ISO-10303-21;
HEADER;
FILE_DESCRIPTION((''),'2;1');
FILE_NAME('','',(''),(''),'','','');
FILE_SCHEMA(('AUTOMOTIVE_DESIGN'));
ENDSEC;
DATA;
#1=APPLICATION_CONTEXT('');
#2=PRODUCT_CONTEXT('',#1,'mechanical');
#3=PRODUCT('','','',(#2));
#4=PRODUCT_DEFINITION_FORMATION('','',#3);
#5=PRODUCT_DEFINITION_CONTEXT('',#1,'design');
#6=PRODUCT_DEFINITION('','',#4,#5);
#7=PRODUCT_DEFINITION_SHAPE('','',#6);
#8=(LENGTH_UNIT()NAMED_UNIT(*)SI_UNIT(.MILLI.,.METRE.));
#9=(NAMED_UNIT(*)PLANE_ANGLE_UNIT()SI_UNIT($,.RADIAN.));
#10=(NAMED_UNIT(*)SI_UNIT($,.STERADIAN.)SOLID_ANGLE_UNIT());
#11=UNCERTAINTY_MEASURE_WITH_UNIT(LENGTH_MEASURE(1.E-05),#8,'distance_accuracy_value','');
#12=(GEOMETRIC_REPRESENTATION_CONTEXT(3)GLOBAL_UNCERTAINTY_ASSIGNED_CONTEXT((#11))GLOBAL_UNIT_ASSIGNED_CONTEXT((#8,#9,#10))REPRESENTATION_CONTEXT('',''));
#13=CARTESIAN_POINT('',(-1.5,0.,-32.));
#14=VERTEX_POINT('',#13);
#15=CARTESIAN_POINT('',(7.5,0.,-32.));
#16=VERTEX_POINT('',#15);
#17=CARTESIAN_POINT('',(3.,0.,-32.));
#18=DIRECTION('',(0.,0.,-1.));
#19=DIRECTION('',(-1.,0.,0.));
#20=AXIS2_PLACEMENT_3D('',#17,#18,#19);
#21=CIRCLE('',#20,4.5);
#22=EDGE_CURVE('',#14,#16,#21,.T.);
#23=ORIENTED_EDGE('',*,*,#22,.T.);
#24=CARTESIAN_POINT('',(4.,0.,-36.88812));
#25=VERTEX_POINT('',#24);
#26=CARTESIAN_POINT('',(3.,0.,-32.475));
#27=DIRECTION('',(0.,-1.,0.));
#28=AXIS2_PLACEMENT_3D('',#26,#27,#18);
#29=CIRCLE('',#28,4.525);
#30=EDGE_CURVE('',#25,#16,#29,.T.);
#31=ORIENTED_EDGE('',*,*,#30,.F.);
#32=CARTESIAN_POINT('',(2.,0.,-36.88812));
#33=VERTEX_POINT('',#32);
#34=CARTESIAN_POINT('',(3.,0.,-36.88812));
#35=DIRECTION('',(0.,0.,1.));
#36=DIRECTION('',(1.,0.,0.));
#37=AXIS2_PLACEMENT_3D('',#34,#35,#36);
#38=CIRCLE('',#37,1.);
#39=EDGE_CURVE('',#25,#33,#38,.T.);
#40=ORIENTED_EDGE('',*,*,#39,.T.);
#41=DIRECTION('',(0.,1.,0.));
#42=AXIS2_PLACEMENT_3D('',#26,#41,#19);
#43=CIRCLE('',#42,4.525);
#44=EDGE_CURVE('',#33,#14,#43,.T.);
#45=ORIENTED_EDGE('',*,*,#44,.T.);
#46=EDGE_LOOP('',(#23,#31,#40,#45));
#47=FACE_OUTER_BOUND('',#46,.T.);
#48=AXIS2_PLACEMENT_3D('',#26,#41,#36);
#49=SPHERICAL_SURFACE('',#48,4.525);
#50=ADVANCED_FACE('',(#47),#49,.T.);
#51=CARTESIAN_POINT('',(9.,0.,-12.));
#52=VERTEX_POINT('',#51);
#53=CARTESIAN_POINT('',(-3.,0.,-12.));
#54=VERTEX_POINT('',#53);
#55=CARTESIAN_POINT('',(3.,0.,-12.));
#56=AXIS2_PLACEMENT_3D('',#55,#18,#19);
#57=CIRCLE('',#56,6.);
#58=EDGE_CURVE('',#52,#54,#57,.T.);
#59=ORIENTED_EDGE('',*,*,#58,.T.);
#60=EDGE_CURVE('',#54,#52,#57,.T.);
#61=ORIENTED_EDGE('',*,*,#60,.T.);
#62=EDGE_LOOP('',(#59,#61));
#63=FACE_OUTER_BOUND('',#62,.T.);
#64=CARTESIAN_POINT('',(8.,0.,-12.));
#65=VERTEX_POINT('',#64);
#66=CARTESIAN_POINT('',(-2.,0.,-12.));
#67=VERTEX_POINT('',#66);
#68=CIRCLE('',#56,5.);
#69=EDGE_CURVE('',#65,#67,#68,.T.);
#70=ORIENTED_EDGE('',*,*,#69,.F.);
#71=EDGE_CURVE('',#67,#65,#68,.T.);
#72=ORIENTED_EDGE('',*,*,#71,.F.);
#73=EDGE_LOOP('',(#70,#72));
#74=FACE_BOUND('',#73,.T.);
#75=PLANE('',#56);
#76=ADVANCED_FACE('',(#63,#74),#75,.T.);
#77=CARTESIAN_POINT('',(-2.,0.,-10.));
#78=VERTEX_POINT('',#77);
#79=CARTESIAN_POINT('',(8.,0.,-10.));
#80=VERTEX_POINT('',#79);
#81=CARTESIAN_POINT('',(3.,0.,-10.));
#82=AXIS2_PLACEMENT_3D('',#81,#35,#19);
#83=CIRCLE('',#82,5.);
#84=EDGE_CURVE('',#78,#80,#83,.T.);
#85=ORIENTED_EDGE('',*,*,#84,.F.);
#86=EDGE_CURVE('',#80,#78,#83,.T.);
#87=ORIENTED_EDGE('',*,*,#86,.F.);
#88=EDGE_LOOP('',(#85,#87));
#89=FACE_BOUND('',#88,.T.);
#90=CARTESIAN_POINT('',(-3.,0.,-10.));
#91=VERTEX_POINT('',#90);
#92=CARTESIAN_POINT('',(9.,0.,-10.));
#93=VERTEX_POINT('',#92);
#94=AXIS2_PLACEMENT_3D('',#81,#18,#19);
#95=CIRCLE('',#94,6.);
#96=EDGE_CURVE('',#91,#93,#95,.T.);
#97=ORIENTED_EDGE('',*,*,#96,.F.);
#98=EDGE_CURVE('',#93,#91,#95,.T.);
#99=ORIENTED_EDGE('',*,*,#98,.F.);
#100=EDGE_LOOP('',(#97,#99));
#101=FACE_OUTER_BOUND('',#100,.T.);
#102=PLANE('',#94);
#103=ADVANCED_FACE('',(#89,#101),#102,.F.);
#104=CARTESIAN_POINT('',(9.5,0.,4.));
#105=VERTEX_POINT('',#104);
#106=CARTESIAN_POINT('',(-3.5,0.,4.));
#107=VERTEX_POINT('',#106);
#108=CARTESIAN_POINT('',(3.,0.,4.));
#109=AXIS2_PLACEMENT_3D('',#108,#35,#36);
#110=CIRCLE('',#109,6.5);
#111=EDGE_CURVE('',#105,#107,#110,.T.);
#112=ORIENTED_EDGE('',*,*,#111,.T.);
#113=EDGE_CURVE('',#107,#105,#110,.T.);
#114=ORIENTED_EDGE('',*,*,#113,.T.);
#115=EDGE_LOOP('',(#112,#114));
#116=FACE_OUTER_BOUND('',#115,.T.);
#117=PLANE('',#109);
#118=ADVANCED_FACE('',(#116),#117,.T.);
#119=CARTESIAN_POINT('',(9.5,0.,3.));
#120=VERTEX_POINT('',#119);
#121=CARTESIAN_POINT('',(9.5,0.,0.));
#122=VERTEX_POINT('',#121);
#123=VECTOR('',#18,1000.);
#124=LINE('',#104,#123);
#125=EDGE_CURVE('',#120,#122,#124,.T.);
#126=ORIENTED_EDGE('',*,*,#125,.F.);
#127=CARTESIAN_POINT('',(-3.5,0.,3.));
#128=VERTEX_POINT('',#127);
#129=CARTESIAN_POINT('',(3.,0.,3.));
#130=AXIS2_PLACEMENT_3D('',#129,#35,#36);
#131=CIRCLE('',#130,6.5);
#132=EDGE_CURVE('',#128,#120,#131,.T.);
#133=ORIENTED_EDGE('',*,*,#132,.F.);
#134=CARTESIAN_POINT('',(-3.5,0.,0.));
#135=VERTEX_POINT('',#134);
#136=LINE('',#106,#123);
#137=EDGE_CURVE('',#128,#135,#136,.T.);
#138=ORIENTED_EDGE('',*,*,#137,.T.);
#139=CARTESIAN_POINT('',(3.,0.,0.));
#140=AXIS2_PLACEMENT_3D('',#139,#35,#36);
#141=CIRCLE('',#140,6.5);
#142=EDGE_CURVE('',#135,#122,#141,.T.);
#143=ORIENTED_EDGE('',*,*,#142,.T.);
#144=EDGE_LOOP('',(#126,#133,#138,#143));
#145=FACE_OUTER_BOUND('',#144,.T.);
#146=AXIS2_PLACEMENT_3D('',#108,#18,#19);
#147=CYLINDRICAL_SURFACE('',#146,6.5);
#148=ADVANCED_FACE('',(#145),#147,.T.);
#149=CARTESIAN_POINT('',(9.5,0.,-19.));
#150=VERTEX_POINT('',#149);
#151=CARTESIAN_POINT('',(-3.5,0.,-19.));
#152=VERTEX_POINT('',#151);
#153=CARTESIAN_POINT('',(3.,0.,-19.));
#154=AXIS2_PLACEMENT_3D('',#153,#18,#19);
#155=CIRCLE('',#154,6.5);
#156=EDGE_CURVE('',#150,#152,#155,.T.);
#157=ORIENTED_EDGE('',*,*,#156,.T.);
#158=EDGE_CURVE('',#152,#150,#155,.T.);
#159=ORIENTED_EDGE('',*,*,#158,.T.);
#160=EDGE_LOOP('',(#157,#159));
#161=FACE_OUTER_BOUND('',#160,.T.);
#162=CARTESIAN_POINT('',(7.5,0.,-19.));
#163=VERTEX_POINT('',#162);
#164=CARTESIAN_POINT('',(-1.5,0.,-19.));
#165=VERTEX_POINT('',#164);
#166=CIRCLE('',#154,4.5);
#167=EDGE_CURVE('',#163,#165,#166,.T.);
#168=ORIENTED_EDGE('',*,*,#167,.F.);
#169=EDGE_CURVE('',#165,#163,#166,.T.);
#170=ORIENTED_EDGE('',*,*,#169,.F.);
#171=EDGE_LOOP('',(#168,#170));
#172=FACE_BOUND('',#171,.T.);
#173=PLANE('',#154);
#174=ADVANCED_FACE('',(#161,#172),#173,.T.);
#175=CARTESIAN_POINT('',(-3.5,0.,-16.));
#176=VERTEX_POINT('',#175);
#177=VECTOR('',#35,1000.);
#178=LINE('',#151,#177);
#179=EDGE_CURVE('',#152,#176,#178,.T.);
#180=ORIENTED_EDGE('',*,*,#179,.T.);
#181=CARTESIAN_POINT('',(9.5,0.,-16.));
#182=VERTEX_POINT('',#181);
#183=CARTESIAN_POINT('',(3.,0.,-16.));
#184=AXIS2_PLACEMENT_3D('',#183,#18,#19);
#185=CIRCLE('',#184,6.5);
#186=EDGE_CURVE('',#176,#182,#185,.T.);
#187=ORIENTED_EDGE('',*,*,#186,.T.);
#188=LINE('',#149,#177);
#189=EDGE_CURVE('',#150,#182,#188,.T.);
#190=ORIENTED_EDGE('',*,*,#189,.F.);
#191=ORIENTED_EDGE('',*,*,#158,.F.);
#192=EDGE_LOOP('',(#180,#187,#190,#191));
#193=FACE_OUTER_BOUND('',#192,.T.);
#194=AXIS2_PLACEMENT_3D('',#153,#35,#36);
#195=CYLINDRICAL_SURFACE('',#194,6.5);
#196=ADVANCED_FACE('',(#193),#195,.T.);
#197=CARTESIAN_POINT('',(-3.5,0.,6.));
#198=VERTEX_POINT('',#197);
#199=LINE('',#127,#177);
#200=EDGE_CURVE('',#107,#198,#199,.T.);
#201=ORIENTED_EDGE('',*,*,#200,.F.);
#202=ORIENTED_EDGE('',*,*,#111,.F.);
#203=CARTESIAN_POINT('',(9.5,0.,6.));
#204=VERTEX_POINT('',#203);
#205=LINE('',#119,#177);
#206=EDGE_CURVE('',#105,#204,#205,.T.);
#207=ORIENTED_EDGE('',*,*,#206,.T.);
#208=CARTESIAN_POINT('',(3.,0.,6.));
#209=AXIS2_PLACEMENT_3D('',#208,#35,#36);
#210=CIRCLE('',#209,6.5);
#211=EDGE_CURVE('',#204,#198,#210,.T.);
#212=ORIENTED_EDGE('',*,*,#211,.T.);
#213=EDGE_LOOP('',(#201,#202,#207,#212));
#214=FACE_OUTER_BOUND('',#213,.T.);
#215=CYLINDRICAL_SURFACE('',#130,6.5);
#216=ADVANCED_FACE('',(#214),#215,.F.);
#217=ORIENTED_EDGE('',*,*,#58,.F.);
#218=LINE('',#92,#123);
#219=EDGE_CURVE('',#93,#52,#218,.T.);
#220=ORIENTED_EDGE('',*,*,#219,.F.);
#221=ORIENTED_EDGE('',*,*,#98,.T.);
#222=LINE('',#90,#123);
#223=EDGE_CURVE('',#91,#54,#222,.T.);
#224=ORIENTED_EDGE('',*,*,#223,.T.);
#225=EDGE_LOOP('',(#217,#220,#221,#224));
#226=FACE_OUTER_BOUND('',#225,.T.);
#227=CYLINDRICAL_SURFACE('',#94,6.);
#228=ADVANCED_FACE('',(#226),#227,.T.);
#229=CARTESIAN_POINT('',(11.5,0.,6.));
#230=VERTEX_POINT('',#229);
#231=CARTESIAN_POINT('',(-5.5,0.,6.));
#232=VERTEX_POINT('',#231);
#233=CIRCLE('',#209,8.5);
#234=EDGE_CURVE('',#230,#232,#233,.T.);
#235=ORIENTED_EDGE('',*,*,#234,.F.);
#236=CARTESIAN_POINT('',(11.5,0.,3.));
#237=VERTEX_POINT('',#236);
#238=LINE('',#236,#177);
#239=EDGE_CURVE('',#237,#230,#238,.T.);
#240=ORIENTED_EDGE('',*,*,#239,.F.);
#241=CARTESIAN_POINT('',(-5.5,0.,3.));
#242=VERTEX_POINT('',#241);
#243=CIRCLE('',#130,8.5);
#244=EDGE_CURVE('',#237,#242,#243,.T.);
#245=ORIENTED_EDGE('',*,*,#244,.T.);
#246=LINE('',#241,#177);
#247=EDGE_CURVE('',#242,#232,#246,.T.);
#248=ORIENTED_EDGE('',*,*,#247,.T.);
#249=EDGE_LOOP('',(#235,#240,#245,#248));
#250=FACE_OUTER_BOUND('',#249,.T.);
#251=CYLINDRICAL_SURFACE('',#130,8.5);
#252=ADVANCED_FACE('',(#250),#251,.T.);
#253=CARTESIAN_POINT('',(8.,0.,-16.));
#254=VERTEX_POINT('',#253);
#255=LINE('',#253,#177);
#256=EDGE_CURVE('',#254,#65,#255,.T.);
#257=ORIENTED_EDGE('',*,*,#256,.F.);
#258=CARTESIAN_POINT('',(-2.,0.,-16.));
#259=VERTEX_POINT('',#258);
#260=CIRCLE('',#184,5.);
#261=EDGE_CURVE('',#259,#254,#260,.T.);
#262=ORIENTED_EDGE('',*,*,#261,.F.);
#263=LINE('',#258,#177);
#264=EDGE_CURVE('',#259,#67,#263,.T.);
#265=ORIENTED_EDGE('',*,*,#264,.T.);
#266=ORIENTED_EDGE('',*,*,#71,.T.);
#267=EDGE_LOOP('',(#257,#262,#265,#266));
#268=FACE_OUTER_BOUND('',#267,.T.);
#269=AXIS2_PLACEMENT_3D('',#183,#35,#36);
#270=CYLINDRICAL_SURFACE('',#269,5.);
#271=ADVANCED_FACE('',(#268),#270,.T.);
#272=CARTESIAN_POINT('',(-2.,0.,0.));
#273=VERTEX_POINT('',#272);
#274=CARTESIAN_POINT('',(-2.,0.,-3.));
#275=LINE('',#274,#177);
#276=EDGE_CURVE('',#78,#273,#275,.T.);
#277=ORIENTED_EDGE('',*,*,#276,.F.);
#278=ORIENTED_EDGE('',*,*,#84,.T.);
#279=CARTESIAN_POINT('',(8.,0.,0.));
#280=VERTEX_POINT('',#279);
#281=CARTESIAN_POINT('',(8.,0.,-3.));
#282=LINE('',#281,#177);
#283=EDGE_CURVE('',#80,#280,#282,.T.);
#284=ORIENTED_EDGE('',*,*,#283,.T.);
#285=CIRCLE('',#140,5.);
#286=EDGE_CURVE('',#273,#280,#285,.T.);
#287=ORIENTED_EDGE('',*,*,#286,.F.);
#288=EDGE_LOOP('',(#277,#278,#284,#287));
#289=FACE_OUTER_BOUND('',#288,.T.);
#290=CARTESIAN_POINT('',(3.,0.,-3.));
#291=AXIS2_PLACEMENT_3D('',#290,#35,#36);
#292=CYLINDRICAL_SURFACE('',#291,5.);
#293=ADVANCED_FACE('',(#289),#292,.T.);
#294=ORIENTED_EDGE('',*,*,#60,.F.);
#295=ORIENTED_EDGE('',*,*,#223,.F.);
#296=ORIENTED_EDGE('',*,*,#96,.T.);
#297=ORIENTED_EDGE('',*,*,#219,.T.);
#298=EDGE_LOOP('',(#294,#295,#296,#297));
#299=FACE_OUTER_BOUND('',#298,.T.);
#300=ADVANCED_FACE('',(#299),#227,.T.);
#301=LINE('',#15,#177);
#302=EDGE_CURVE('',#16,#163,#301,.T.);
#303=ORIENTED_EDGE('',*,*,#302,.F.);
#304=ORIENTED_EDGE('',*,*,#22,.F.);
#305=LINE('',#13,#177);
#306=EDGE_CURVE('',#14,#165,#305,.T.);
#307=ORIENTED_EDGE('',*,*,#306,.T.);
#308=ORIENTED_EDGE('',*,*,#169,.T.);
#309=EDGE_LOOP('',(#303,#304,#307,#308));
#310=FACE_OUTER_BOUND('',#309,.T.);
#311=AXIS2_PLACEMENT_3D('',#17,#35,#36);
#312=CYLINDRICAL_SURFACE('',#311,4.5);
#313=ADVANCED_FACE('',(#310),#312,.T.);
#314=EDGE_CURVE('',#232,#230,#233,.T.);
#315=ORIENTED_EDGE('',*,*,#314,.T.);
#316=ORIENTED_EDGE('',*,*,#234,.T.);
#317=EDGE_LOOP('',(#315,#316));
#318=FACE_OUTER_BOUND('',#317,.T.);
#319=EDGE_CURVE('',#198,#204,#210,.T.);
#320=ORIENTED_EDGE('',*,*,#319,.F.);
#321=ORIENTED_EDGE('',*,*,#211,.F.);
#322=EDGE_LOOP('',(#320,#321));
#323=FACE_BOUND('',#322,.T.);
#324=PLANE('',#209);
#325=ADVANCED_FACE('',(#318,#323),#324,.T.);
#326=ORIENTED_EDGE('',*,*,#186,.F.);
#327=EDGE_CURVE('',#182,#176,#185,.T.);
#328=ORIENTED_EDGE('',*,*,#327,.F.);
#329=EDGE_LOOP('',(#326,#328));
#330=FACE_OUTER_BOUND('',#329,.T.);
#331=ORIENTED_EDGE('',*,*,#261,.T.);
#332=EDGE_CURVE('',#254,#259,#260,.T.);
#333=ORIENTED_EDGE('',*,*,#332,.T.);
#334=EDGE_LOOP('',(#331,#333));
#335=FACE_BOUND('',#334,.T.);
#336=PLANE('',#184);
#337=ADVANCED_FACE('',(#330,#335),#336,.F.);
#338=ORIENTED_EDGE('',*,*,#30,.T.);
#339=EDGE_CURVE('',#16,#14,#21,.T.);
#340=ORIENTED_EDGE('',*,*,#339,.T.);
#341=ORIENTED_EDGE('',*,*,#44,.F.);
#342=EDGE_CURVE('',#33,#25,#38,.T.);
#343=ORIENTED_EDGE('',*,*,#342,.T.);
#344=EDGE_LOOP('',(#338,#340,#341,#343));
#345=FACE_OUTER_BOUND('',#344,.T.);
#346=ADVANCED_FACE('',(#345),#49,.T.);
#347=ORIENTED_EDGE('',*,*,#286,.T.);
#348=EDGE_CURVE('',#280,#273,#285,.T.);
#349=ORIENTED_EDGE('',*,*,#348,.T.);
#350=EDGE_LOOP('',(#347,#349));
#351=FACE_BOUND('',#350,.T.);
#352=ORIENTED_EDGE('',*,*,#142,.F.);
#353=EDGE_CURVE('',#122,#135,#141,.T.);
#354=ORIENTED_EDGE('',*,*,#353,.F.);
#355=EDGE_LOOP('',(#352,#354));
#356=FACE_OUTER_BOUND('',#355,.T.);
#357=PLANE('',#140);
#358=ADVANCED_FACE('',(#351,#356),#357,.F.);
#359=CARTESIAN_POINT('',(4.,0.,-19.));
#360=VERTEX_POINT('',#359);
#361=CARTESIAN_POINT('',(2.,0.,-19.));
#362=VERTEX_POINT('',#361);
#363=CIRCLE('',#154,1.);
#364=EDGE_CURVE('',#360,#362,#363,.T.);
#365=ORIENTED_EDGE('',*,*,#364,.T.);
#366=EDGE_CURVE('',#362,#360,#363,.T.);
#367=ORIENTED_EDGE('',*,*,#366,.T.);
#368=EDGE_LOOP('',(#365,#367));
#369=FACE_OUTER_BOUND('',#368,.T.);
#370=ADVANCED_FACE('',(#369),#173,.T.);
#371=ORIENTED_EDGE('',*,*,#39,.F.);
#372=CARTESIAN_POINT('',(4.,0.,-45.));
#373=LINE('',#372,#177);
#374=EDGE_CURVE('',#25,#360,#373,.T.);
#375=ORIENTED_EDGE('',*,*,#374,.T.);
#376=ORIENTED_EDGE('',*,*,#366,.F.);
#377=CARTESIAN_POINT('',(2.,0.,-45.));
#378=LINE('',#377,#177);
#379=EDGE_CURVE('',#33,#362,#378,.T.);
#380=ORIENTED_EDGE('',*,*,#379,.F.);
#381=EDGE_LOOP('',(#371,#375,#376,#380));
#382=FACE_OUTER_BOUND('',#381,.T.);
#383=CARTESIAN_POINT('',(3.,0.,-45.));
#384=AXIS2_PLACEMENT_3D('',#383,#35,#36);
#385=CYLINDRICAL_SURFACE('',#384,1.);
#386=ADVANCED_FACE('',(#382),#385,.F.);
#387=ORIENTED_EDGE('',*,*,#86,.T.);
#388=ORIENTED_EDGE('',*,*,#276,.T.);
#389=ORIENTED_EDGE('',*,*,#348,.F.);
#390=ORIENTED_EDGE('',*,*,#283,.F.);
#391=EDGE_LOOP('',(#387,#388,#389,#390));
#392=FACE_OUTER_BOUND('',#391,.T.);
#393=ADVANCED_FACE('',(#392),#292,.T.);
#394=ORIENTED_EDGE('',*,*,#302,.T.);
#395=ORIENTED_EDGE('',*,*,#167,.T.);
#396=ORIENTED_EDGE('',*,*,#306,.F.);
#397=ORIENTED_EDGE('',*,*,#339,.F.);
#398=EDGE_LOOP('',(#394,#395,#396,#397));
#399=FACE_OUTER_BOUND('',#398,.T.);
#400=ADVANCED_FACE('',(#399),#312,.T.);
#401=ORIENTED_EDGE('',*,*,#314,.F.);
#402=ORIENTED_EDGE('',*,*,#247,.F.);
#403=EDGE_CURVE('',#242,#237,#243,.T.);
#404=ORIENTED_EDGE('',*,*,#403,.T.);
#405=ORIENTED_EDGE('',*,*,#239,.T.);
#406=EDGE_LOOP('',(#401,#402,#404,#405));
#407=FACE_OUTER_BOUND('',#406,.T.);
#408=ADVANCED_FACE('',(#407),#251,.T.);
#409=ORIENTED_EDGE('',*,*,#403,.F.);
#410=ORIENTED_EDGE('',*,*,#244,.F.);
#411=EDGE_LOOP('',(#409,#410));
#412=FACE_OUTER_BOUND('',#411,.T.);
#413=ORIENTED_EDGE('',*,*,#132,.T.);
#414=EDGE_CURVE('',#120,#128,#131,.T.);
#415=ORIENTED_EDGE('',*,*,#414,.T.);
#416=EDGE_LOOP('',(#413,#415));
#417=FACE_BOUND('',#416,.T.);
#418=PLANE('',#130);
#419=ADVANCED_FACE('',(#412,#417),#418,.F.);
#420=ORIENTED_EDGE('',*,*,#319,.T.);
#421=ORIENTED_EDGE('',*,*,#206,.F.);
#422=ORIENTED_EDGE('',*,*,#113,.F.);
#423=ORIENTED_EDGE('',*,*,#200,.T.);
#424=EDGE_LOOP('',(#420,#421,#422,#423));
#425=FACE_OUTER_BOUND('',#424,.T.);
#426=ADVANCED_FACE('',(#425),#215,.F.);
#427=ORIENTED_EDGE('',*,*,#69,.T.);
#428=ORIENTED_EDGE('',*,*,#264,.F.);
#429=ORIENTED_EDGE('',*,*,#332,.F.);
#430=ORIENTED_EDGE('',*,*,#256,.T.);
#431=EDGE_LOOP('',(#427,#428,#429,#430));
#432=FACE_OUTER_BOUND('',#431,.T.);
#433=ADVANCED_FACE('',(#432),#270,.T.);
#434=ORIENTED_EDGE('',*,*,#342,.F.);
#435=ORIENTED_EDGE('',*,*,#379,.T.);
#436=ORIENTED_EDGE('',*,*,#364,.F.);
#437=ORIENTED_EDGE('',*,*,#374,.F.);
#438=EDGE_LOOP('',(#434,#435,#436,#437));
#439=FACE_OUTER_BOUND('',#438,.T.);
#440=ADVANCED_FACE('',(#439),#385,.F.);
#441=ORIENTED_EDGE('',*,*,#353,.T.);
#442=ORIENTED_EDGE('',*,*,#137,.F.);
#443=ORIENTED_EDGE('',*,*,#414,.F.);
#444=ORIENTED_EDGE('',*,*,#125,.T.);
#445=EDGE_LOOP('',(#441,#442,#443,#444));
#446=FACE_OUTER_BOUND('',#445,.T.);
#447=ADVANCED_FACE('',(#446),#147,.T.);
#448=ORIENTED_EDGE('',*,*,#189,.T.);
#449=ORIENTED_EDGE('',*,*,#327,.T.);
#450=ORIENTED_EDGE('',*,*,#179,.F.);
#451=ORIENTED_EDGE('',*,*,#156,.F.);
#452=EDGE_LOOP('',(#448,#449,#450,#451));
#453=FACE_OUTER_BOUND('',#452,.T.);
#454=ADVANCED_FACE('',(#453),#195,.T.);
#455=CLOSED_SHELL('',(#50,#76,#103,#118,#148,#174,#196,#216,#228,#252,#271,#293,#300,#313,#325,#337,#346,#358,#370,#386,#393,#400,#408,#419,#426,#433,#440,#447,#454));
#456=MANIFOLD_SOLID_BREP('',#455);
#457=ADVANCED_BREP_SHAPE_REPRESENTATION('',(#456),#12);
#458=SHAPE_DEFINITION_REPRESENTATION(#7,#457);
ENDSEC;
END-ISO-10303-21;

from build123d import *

# Parameters (mm, degrees)
SKETCH1_R                = 5
BOSS_EXTRUDE1_DEPTH      = 3
SKETCH2_R                = 6.5
BOSS_EXTRUDE2_DEPTH      = 4
BOSS_EXTRUDE3_DEPTH      = 2
BOSS_EXTRUDE3_DEPTH_BACK = 1
SKETCH3_R                = 8.5
SKETCH3_R_2              = 6.5
SKETCH4_R                = 5
BOSS_EXTRUDE4_DEPTH      = 9
SKETCH5_R                = 6
BOSS_EXTRUDE5_DEPTH      = 2
SKETCH7_R                = 5
BOSS_EXTRUDE6_DEPTH      = 4
BOSS_EXTRUDE7_START      = 3
SKETCH8_R                = 6.5
BOSS_EXTRUDE7_DEPTH      = 3
SKETCH10_R               = 4.5
BOSS_EXTRUDE8_DEPTH      = 13
DOME1_FACE_RADIUS        = 4.5
DOME1_HEIGHT             = 5
SKETCH11_R               = 1
CUT_EXTRUDE1_DEPTH       = 26


with BuildPart() as part:
    # Sketch1 → Boss-Extrude1 (new body)
    with BuildSketch(Plane.XY):
        with Locations((3, 0)):
            Circle(SKETCH1_R)
    extrude(amount=-BOSS_EXTRUDE1_DEPTH)

    # Sketch2 → Boss-Extrude2 (add)
    with BuildSketch(Plane.XY):
        with Locations((3, 0)):
            Circle(SKETCH2_R)
    extrude(amount=BOSS_EXTRUDE2_DEPTH)

    # Sketch3 → Boss-Extrude3 (add, two sides: drawn at the far end of the back side and taken through both)
    with BuildSketch(Plane.XY.offset(4).offset(-BOSS_EXTRUDE3_DEPTH_BACK)):
        with Locations((3, 0)):
            Circle(SKETCH3_R)
        with Locations((3, 0)):
            Circle(SKETCH3_R_2, mode=Mode.SUBTRACT)
    extrude(amount=BOSS_EXTRUDE3_DEPTH + BOSS_EXTRUDE3_DEPTH_BACK)

    # Sketch4 → Boss-Extrude4 (add)
    with BuildSketch(Plane(origin=(0, 0, -3), x_dir=(-1, 0, 0), z_dir=(0, 0, -1))):
        with Locations(Location((-3, 0, 0), (0, 0, 180))):
            Circle(SKETCH4_R)
    extrude(amount=BOSS_EXTRUDE4_DEPTH)

    # Sketch5 → Boss-Extrude5 (add)
    with BuildSketch(Plane(origin=(0, 0, -12), x_dir=(-1, 0, 0), z_dir=(0, 0, -1))):
        with Locations((-3, 0)):
            Circle(SKETCH5_R)
    extrude(amount=-BOSS_EXTRUDE5_DEPTH)

    # Sketch7 → Boss-Extrude6 (add)
    with BuildSketch(Plane(origin=(0, 0, -12), x_dir=(-1, 0, 0), z_dir=(0, 0, -1))):
        with Locations(Location((-3, 0, 0), (0, 0, 180))):
            Circle(SKETCH7_R)
    extrude(amount=BOSS_EXTRUDE6_DEPTH)

    # Sketch8 → Boss-Extrude7 (add)
    with BuildSketch(Plane(origin=(0, 0, -16), x_dir=(-1, 0, 0), z_dir=(0, 0, -1)).offset(BOSS_EXTRUDE7_START)):
        with Locations(Location((-3, 0, 0), (0, 0, 180))):
            Circle(SKETCH8_R)
    extrude(amount=-BOSS_EXTRUDE7_DEPTH)

    # Sketch10 → Boss-Extrude8 (add)
    with BuildSketch(Plane(origin=(0, 0, -19), x_dir=(-1, 0, 0), z_dir=(0, 0, -1))):
        with Locations((-3, 0)):
            Circle(SKETCH10_R)
    extrude(amount=BOSS_EXTRUDE8_DEPTH)

    # Dome1: a dome of height H over a round flat face of radius A is a cap of a sphere of radius (A * A + H * H) / (2 * H)
    dome1_r = (DOME1_FACE_RADIUS * DOME1_FACE_RADIUS + DOME1_HEIGHT * DOME1_HEIGHT) / (2 * DOME1_HEIGHT)
    dome1_base = Plane((3, 0, -32), z_dir=(0, 0, -1))
    with Locations(dome1_base.offset(DOME1_HEIGHT - dome1_r)):
        dome1_ball = Sphere(dome1_r, mode=Mode.PRIVATE)
    add(split(dome1_ball, bisect_by=dome1_base, keep=Keep.TOP, mode=Mode.PRIVATE))

    # Sketch11 → Cut-Extrude1 (cut)
    with BuildSketch(Plane(origin=(0, 0, -19), x_dir=(-1, 0, 0), z_dir=(0, 0, -1))):
        with Locations(Location((-3, 0, 0), (0, 0, 180))):
            Circle(SKETCH11_R)
    extrude(amount=CUT_EXTRUDE1_DEPTH, mode=Mode.SUBTRACT)


solid = part.part
